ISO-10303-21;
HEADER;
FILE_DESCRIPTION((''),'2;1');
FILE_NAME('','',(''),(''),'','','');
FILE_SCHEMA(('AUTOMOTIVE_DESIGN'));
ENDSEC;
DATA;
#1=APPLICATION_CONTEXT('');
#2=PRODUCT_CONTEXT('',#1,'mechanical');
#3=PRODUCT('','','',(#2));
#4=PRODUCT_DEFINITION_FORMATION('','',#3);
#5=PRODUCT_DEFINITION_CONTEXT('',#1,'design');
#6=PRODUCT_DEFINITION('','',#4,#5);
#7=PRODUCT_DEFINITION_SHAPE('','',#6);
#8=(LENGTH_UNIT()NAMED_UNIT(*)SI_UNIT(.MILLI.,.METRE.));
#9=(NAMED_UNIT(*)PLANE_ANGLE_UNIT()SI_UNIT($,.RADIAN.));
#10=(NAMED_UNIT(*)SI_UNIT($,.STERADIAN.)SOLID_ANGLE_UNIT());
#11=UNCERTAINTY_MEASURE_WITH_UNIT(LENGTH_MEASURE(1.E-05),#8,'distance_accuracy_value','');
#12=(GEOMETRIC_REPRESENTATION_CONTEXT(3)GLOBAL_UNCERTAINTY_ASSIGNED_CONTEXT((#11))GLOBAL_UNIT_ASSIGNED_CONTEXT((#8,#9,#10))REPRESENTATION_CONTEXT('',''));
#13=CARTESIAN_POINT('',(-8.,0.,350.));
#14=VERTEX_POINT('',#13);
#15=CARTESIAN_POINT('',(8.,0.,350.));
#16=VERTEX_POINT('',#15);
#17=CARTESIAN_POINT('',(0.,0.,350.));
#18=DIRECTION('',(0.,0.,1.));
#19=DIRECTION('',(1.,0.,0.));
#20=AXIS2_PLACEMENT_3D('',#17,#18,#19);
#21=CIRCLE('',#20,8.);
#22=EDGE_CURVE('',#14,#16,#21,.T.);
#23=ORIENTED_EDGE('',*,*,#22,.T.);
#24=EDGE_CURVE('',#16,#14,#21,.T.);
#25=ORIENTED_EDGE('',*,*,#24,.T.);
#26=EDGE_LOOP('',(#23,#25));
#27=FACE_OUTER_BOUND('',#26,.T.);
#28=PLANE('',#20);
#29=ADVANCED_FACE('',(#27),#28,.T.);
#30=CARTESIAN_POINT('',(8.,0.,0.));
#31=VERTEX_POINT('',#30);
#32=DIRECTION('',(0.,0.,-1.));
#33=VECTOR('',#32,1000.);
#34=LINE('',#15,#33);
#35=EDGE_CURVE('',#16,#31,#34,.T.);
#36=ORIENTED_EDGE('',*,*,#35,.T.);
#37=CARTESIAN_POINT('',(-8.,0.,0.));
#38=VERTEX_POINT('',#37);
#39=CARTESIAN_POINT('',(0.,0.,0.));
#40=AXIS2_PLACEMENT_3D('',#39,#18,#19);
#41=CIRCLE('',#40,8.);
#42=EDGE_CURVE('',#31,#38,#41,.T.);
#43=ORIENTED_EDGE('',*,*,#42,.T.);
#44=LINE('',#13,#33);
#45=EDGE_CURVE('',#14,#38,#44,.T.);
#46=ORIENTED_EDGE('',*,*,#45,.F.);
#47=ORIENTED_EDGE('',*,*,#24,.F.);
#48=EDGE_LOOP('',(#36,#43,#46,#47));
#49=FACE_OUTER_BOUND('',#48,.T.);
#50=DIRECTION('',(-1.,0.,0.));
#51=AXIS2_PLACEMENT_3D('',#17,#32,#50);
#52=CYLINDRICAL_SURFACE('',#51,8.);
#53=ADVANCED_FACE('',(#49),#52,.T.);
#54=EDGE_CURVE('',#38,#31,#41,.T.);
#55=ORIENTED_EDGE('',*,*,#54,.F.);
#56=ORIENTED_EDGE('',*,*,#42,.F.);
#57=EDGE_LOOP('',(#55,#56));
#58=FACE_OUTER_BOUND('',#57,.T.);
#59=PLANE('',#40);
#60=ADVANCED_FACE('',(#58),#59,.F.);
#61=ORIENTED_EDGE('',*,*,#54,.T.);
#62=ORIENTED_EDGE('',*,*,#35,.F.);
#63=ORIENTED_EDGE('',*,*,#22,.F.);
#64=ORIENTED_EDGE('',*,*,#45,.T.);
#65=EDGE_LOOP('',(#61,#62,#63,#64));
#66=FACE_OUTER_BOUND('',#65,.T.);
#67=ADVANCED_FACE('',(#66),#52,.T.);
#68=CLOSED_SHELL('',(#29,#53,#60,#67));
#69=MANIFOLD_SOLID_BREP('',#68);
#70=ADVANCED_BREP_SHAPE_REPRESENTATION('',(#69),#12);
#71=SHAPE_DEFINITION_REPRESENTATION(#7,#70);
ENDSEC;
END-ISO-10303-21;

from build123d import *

# Parameters (mm, degrees)
SKETCH_1_R      = 8
EXTRUDE_1_DEPTH = 350


with BuildPart() as part:
    # 草图1 → 凸台-拉伸1 (new body)
    with BuildSketch(Plane.XY):
        Circle(SKETCH_1_R)
    extrude(amount=EXTRUDE_1_DEPTH)


solid = part.part
